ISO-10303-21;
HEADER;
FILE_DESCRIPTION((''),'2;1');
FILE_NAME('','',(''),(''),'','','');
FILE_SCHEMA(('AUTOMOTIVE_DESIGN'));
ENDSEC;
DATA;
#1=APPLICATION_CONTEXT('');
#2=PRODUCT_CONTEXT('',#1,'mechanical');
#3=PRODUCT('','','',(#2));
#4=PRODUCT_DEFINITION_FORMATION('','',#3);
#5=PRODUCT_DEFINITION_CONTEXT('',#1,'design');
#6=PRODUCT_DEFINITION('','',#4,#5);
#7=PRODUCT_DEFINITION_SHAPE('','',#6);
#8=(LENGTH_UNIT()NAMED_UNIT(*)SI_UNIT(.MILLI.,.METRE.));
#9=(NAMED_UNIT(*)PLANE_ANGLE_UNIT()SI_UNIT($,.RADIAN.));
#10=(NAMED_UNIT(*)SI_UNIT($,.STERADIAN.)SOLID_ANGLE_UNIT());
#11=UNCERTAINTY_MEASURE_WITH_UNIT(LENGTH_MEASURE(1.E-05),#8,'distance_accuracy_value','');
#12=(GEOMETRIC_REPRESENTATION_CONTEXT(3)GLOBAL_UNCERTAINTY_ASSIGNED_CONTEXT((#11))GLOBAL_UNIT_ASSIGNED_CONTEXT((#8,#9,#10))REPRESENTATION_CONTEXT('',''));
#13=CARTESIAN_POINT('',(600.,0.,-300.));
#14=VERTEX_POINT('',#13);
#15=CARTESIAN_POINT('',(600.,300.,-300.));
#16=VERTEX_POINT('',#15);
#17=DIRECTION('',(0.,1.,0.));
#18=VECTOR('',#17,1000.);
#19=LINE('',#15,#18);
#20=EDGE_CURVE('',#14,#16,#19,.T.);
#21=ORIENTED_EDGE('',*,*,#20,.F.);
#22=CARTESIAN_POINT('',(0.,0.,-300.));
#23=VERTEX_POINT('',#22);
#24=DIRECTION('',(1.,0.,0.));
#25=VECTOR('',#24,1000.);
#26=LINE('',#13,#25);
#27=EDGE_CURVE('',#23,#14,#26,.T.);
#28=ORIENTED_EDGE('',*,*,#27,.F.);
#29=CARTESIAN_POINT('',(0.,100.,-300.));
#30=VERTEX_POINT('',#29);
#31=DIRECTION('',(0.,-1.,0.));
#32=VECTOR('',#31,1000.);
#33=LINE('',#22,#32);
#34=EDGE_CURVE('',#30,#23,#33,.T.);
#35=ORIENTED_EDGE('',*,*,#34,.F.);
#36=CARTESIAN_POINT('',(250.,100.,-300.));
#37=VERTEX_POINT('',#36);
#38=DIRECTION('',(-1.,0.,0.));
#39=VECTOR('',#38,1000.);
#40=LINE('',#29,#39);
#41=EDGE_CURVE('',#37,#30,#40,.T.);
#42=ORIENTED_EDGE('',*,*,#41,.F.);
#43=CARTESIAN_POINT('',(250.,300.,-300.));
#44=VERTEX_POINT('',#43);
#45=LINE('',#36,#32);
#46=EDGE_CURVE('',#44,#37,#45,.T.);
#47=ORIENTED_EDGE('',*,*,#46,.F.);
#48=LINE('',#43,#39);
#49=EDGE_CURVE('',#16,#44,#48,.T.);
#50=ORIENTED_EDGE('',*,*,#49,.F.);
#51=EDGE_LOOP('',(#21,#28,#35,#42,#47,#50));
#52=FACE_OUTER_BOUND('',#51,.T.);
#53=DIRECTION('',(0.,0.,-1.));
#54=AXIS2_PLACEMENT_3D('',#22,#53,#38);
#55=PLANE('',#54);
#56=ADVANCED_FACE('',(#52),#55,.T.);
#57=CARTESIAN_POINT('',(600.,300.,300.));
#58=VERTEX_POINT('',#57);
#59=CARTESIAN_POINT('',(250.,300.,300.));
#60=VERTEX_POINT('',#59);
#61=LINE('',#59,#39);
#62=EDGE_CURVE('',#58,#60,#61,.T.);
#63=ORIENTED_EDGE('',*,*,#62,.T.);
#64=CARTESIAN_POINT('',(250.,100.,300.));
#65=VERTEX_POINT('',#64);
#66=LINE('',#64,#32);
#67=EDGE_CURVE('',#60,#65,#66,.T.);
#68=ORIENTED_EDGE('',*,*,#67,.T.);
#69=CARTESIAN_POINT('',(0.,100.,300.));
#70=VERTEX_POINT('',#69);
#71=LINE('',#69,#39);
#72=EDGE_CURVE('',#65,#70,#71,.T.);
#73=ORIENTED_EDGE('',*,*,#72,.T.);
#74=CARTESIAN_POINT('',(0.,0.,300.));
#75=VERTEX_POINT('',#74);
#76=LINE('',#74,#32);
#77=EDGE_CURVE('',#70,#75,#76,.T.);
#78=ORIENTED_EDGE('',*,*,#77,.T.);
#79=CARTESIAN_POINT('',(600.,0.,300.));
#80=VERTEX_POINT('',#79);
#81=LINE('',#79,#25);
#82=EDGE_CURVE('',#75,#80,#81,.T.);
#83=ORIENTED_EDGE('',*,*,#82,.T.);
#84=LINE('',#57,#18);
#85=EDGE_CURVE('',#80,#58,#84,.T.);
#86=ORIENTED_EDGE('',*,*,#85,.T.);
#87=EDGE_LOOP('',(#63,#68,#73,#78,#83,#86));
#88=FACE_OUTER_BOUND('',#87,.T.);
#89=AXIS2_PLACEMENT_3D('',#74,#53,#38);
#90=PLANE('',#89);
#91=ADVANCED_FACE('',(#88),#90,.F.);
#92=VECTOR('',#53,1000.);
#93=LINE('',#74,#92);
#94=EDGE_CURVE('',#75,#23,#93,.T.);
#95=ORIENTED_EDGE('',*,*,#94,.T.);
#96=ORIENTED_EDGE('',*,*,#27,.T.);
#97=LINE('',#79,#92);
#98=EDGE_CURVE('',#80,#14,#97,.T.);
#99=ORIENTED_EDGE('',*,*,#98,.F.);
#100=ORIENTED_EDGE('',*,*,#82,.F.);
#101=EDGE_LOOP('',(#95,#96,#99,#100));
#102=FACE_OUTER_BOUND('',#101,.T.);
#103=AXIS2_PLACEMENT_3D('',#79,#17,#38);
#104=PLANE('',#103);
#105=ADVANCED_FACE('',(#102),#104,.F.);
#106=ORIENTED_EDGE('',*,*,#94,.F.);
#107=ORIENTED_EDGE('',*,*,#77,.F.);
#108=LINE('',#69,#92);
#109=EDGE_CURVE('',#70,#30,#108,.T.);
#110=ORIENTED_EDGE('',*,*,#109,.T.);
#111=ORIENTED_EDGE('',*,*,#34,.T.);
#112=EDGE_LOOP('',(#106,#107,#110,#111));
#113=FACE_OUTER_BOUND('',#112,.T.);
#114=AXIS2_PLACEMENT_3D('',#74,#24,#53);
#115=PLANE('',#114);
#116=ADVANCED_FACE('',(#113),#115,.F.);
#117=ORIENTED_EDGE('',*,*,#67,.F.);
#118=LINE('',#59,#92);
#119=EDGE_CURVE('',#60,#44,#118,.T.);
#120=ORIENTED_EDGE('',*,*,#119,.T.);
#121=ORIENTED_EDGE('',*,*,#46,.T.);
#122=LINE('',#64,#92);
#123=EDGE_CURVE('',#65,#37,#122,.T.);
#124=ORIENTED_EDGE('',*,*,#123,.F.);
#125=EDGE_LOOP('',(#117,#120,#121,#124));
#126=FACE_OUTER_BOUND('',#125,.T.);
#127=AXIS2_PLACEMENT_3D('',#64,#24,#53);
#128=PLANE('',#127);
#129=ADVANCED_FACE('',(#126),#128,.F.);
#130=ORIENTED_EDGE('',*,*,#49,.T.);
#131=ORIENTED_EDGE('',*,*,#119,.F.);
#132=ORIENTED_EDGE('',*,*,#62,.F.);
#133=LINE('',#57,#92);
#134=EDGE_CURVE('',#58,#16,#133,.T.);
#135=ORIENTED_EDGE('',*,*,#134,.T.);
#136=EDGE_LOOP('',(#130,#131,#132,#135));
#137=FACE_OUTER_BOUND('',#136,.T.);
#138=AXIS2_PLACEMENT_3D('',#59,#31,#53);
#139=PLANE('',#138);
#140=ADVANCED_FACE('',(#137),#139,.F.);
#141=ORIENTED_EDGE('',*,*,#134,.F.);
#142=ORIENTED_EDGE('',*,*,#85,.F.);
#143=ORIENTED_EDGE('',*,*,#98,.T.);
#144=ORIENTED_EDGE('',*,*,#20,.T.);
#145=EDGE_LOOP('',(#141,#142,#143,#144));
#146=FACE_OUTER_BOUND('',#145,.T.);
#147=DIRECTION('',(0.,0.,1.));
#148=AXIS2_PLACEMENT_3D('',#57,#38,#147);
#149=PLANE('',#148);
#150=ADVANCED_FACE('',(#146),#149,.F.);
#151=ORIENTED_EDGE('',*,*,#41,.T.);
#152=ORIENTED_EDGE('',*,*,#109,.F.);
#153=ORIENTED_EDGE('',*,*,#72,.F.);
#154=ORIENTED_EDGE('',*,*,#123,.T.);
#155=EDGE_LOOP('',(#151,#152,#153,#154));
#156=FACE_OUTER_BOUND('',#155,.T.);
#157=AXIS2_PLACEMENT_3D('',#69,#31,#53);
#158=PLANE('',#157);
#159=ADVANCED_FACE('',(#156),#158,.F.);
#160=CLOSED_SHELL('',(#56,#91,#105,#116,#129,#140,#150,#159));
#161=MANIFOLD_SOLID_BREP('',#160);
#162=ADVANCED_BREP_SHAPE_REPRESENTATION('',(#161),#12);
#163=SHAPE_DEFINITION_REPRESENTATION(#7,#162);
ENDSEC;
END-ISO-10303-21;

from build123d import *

# Parameters (mm, degrees)
EXTRUDE_1_DEPTH = 300


with BuildPart() as part:
    # 草图1 → 凸台-拉伸1 (new, symmetric)
    with BuildSketch(Plane.XY):
        Polygon((0, 0), (0, 100), (250, 100), (250, 300), (600, 300), (600, 0), align=None)
    extrude(amount=EXTRUDE_1_DEPTH, both=True)


solid = part.part
